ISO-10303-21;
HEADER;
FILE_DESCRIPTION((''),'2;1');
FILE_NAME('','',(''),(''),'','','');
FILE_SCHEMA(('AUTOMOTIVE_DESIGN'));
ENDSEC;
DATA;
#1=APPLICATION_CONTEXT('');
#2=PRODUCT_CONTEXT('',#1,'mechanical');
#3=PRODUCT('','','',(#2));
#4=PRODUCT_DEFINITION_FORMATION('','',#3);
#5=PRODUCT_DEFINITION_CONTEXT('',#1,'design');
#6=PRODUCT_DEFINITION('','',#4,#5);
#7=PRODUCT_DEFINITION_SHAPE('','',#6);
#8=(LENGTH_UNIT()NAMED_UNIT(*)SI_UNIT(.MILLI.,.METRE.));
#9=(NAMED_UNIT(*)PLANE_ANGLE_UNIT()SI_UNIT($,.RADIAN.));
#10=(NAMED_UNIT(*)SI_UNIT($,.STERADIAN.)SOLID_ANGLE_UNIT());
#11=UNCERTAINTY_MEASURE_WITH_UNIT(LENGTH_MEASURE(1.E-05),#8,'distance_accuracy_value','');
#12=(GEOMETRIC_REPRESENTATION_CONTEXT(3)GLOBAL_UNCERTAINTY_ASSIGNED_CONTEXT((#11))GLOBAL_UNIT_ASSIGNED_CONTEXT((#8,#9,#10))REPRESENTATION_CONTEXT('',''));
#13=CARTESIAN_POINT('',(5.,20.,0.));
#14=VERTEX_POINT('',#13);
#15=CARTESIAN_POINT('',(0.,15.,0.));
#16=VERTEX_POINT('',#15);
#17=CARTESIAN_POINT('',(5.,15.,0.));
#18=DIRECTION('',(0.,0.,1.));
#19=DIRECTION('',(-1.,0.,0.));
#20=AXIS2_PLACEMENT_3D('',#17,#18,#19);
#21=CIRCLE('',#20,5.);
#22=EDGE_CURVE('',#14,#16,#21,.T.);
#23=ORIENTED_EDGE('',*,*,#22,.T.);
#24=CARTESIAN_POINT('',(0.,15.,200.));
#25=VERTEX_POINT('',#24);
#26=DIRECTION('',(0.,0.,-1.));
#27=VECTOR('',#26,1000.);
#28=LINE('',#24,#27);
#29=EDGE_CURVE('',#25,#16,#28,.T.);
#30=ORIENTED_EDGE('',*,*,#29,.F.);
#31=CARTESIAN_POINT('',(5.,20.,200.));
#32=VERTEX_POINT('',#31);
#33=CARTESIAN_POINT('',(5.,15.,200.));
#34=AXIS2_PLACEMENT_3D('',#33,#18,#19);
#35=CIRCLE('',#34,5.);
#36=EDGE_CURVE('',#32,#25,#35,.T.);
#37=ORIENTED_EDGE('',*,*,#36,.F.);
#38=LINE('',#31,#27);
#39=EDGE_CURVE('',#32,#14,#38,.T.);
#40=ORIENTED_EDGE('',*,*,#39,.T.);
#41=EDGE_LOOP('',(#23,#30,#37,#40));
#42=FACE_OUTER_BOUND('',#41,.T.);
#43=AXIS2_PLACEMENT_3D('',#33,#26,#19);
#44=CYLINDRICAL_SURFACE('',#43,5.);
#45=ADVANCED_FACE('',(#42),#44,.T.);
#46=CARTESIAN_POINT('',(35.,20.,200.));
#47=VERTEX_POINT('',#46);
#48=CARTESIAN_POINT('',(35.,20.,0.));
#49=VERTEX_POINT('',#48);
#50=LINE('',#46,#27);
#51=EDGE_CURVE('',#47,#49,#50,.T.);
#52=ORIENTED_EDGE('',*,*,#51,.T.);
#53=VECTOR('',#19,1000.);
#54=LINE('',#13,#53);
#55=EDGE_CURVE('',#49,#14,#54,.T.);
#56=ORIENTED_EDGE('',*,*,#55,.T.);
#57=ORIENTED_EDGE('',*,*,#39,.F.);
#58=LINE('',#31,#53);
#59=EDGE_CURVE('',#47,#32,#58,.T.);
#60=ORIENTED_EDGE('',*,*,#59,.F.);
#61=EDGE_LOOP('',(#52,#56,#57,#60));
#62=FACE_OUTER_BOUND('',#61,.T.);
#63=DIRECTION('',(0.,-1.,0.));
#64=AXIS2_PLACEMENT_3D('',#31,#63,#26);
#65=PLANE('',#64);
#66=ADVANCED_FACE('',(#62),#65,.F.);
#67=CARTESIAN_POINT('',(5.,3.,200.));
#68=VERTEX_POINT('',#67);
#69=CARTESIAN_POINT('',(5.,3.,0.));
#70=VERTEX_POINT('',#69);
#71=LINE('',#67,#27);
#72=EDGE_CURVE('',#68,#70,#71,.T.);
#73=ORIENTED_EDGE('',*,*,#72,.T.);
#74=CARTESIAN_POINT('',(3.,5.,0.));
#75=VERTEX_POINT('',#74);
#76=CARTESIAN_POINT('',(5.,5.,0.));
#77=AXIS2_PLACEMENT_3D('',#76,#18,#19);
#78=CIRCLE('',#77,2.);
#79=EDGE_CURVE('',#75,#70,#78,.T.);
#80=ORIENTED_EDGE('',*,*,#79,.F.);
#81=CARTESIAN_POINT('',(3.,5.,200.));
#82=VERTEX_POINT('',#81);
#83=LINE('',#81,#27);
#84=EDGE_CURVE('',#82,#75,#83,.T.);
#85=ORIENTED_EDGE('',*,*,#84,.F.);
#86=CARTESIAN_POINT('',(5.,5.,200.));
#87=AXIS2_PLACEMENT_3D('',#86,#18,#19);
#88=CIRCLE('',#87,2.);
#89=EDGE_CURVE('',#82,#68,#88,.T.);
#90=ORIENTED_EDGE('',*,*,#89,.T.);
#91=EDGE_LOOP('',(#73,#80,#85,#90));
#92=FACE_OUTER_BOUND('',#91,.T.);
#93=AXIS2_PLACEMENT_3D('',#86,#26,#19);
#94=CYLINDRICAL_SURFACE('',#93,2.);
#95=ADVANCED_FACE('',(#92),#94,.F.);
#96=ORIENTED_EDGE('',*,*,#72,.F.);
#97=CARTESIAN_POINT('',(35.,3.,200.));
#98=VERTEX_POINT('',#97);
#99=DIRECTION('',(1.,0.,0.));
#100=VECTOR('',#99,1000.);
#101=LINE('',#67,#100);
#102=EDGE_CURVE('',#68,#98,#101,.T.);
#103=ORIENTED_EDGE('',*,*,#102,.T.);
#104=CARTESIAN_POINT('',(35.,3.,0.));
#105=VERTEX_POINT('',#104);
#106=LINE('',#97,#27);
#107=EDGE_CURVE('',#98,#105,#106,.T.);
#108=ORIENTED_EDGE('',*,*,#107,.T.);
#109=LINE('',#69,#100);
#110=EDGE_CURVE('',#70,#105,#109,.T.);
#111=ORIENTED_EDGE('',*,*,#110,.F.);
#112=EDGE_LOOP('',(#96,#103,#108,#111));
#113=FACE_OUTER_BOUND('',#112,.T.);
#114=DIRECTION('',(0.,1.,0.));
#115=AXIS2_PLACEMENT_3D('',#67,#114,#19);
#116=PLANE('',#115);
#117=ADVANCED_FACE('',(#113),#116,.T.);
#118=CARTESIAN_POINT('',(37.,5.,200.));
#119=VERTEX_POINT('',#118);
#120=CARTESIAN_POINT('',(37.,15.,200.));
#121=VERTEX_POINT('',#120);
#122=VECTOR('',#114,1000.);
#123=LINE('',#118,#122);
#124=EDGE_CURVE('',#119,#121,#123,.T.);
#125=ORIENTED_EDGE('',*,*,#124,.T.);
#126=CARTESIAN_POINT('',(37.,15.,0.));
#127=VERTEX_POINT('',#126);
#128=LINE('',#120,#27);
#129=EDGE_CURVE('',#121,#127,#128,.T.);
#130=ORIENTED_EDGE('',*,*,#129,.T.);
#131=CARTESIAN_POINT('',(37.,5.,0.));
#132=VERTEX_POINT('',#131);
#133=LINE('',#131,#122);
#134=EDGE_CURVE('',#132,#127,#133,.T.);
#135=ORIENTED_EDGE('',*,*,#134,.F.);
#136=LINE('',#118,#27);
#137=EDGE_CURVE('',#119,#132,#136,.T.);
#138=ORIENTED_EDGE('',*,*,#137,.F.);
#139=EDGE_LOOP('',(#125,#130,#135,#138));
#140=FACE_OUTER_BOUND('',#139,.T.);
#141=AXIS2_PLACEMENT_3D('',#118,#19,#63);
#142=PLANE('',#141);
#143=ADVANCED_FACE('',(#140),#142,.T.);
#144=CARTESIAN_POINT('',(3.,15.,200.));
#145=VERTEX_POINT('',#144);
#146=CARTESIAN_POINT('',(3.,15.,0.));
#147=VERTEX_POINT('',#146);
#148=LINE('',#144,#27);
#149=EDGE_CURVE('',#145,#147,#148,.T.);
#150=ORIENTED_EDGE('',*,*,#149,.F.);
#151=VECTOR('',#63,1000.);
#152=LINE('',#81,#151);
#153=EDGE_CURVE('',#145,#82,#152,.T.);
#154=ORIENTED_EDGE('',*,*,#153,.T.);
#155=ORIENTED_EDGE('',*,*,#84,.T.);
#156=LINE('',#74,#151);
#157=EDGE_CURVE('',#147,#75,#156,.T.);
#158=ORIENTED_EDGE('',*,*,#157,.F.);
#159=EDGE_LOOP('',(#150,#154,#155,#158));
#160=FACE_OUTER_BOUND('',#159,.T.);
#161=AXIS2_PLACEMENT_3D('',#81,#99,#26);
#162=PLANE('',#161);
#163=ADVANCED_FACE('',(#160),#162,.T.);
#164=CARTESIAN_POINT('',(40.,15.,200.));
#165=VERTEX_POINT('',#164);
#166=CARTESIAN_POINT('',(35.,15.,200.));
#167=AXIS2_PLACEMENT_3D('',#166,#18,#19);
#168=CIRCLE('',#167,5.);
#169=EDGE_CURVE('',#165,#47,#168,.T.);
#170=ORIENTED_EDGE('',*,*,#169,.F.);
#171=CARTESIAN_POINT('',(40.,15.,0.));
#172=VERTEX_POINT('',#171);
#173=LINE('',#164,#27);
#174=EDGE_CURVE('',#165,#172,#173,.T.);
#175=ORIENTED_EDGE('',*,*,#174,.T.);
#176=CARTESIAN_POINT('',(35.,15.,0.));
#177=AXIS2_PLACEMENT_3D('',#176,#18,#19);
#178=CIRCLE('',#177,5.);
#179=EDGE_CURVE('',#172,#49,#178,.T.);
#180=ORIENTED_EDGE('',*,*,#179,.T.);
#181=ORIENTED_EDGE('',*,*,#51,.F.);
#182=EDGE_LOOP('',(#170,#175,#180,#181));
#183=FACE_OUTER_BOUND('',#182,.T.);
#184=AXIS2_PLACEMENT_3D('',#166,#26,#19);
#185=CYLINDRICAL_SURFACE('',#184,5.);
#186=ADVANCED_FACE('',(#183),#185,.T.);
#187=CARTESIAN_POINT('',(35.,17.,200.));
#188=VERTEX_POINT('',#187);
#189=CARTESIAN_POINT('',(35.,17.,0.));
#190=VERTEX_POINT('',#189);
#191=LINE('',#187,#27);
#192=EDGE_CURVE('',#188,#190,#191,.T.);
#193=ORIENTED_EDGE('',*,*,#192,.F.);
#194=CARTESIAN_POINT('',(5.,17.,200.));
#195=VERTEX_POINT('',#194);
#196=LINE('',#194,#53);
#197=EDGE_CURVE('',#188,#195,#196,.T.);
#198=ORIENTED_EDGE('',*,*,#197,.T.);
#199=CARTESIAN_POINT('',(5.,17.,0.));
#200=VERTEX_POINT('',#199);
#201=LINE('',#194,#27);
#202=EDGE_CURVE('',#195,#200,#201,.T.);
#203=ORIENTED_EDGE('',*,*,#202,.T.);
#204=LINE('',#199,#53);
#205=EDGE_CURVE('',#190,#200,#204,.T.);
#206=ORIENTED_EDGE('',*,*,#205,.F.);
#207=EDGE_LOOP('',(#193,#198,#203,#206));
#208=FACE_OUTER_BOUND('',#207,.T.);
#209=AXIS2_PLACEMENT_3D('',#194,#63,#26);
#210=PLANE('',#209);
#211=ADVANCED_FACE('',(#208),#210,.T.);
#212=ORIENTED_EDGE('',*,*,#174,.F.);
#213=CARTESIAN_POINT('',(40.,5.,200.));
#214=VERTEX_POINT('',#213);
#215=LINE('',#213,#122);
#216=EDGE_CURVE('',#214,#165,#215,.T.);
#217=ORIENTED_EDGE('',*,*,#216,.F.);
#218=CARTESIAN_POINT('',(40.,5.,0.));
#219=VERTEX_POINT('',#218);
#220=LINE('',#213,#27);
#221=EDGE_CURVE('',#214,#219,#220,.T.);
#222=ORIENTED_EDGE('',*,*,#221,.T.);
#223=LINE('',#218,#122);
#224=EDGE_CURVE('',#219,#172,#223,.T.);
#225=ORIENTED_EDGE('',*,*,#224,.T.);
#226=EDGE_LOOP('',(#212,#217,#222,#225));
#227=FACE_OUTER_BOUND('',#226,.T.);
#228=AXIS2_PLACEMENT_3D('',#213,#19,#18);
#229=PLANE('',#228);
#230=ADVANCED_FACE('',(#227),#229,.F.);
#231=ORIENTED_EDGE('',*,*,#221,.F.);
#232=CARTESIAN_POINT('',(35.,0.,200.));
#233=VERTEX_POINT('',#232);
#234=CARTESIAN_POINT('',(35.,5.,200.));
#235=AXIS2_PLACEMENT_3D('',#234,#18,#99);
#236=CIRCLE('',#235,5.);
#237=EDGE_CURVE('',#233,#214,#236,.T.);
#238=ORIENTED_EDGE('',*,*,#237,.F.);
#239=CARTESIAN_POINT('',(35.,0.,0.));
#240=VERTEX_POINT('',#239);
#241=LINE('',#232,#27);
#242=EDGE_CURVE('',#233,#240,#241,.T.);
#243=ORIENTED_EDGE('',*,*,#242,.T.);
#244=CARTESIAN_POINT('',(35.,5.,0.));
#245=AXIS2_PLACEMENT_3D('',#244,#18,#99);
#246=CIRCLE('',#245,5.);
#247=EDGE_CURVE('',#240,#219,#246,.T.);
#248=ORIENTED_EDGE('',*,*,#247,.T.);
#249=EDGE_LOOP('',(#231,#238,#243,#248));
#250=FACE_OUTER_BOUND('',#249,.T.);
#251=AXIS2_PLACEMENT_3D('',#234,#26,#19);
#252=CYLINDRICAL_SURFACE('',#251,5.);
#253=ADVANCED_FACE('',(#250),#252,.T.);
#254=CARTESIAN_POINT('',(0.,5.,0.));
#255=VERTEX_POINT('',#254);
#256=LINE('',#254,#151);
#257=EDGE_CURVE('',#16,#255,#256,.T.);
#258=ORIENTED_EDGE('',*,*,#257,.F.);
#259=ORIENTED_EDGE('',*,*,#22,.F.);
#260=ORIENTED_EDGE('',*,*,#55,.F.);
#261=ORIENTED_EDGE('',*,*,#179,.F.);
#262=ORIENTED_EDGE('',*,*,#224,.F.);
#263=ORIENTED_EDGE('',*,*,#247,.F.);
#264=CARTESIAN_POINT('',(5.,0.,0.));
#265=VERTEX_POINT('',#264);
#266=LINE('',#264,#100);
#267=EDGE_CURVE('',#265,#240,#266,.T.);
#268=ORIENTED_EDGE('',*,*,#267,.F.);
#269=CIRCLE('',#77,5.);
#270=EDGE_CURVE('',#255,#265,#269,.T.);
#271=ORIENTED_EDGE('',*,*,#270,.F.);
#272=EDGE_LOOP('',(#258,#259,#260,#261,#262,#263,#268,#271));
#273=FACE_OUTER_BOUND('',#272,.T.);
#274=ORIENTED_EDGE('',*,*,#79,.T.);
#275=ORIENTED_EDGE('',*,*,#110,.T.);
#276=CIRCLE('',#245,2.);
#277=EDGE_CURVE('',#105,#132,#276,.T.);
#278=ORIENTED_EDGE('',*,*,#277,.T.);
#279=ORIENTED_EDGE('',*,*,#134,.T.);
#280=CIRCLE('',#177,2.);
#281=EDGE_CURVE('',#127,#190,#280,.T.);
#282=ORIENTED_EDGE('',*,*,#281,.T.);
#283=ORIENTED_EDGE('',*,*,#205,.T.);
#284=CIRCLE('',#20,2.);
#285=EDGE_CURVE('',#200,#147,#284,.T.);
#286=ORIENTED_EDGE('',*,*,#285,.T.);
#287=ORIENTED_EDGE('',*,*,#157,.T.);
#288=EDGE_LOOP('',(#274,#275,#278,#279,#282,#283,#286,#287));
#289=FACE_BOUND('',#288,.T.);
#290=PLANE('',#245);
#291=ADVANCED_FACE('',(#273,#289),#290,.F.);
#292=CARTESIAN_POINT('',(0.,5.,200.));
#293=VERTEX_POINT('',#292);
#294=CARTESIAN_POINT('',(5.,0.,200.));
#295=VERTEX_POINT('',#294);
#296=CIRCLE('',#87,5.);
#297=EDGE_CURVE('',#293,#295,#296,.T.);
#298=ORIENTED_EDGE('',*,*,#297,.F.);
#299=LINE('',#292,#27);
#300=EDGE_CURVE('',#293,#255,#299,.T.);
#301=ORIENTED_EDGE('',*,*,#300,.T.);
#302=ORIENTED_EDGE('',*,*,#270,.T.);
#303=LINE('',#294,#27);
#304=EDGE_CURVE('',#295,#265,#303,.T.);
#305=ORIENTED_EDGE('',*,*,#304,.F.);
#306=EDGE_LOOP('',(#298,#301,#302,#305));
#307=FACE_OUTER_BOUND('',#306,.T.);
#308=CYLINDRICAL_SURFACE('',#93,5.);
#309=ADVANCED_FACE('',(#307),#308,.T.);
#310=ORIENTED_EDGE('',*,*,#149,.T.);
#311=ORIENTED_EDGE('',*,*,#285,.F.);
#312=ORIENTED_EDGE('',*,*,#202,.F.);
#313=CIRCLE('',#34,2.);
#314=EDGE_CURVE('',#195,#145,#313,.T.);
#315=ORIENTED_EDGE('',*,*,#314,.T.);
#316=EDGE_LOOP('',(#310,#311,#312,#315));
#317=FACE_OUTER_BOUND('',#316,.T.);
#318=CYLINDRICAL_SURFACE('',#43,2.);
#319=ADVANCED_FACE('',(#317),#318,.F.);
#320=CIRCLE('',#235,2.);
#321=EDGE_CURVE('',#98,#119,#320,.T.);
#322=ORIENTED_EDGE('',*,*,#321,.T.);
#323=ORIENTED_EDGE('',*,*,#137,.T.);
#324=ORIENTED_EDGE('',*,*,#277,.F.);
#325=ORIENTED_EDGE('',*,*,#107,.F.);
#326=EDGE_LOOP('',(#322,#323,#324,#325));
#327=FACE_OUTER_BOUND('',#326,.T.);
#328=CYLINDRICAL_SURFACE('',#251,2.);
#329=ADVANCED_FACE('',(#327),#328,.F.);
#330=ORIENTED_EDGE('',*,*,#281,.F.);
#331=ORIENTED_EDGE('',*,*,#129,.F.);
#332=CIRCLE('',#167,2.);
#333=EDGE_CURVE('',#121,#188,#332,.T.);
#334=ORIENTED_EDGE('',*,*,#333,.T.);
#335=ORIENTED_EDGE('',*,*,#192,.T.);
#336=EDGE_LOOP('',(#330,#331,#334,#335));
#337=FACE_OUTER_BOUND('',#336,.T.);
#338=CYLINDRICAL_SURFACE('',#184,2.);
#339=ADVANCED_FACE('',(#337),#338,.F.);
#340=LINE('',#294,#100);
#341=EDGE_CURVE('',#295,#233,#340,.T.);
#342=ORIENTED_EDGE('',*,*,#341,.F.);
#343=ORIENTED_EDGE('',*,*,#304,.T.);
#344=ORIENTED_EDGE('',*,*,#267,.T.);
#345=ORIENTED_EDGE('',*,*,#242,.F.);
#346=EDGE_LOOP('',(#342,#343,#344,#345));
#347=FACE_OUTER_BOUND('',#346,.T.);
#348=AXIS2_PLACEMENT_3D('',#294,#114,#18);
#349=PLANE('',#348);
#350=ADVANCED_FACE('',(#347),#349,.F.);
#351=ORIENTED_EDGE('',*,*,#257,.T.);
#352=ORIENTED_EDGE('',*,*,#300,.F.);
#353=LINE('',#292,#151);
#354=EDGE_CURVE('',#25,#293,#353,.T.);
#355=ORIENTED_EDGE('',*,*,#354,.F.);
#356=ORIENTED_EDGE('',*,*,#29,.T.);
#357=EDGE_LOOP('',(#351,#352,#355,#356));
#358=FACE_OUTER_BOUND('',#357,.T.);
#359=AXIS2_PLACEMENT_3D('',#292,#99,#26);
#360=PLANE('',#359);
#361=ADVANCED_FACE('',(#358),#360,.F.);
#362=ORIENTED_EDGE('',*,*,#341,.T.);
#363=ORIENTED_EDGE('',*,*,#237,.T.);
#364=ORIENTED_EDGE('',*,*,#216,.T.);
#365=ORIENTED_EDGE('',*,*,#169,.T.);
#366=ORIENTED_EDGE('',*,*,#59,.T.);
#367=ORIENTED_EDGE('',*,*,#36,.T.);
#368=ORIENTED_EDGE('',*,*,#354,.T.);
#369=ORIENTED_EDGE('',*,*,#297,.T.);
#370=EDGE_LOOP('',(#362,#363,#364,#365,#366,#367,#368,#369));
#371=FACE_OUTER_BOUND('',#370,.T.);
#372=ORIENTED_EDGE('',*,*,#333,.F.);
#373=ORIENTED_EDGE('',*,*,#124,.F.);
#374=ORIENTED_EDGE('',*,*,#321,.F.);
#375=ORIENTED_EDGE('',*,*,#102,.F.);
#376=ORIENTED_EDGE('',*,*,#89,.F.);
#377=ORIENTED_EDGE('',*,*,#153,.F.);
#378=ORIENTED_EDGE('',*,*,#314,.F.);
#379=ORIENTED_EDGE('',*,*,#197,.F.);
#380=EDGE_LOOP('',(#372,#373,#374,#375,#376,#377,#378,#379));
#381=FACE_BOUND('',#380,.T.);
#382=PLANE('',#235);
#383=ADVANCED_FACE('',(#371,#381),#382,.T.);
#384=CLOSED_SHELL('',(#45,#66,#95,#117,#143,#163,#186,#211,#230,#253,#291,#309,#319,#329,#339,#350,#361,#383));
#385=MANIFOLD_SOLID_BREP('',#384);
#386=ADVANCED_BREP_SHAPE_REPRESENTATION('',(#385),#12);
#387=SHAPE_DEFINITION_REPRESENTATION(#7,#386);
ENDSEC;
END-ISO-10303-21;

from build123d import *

# Parameters (mm, degrees)
BOSS_EXTRUDE1_DEPTH = 200


with BuildPart() as part:
    # Sketch1 → Boss-Extrude1 (new body)
    with BuildSketch(Plane.XY):
        with BuildLine():
            Line((5, 0), (35, 0))
            ThreePointArc((35, 0), (38.535533906, 1.464466094), (40, 5))
            Line((40, 5), (40, 15))
            ThreePointArc((40, 15), (38.535533906, 18.535533906), (35, 20))
            Line((35, 20), (5, 20))
            ThreePointArc((5, 20), (1.464466094, 18.535533906), (0, 15))
            Line((0, 15), (0, 5))
            ThreePointArc((0, 5), (1.464466094, 1.464466094), (5, 0))
        make_face()
        with BuildLine():
            Line((5, 17), (35, 17))
            ThreePointArc((35, 17), (36.414213562, 16.414213562), (37, 15))
            Line((37, 15), (37, 5))
            ThreePointArc((37, 5), (36.414213562, 3.585786438), (35, 3))
            Line((35, 3), (5, 3))
            ThreePointArc((5, 3), (3.585786438, 3.585786438), (3, 5))
            Line((3, 5), (3, 15))
            ThreePointArc((3, 15), (3.585786438, 16.414213562), (5, 17))
        make_face(mode=Mode.SUBTRACT)
    extrude(amount=BOSS_EXTRUDE1_DEPTH)


solid = part.part
